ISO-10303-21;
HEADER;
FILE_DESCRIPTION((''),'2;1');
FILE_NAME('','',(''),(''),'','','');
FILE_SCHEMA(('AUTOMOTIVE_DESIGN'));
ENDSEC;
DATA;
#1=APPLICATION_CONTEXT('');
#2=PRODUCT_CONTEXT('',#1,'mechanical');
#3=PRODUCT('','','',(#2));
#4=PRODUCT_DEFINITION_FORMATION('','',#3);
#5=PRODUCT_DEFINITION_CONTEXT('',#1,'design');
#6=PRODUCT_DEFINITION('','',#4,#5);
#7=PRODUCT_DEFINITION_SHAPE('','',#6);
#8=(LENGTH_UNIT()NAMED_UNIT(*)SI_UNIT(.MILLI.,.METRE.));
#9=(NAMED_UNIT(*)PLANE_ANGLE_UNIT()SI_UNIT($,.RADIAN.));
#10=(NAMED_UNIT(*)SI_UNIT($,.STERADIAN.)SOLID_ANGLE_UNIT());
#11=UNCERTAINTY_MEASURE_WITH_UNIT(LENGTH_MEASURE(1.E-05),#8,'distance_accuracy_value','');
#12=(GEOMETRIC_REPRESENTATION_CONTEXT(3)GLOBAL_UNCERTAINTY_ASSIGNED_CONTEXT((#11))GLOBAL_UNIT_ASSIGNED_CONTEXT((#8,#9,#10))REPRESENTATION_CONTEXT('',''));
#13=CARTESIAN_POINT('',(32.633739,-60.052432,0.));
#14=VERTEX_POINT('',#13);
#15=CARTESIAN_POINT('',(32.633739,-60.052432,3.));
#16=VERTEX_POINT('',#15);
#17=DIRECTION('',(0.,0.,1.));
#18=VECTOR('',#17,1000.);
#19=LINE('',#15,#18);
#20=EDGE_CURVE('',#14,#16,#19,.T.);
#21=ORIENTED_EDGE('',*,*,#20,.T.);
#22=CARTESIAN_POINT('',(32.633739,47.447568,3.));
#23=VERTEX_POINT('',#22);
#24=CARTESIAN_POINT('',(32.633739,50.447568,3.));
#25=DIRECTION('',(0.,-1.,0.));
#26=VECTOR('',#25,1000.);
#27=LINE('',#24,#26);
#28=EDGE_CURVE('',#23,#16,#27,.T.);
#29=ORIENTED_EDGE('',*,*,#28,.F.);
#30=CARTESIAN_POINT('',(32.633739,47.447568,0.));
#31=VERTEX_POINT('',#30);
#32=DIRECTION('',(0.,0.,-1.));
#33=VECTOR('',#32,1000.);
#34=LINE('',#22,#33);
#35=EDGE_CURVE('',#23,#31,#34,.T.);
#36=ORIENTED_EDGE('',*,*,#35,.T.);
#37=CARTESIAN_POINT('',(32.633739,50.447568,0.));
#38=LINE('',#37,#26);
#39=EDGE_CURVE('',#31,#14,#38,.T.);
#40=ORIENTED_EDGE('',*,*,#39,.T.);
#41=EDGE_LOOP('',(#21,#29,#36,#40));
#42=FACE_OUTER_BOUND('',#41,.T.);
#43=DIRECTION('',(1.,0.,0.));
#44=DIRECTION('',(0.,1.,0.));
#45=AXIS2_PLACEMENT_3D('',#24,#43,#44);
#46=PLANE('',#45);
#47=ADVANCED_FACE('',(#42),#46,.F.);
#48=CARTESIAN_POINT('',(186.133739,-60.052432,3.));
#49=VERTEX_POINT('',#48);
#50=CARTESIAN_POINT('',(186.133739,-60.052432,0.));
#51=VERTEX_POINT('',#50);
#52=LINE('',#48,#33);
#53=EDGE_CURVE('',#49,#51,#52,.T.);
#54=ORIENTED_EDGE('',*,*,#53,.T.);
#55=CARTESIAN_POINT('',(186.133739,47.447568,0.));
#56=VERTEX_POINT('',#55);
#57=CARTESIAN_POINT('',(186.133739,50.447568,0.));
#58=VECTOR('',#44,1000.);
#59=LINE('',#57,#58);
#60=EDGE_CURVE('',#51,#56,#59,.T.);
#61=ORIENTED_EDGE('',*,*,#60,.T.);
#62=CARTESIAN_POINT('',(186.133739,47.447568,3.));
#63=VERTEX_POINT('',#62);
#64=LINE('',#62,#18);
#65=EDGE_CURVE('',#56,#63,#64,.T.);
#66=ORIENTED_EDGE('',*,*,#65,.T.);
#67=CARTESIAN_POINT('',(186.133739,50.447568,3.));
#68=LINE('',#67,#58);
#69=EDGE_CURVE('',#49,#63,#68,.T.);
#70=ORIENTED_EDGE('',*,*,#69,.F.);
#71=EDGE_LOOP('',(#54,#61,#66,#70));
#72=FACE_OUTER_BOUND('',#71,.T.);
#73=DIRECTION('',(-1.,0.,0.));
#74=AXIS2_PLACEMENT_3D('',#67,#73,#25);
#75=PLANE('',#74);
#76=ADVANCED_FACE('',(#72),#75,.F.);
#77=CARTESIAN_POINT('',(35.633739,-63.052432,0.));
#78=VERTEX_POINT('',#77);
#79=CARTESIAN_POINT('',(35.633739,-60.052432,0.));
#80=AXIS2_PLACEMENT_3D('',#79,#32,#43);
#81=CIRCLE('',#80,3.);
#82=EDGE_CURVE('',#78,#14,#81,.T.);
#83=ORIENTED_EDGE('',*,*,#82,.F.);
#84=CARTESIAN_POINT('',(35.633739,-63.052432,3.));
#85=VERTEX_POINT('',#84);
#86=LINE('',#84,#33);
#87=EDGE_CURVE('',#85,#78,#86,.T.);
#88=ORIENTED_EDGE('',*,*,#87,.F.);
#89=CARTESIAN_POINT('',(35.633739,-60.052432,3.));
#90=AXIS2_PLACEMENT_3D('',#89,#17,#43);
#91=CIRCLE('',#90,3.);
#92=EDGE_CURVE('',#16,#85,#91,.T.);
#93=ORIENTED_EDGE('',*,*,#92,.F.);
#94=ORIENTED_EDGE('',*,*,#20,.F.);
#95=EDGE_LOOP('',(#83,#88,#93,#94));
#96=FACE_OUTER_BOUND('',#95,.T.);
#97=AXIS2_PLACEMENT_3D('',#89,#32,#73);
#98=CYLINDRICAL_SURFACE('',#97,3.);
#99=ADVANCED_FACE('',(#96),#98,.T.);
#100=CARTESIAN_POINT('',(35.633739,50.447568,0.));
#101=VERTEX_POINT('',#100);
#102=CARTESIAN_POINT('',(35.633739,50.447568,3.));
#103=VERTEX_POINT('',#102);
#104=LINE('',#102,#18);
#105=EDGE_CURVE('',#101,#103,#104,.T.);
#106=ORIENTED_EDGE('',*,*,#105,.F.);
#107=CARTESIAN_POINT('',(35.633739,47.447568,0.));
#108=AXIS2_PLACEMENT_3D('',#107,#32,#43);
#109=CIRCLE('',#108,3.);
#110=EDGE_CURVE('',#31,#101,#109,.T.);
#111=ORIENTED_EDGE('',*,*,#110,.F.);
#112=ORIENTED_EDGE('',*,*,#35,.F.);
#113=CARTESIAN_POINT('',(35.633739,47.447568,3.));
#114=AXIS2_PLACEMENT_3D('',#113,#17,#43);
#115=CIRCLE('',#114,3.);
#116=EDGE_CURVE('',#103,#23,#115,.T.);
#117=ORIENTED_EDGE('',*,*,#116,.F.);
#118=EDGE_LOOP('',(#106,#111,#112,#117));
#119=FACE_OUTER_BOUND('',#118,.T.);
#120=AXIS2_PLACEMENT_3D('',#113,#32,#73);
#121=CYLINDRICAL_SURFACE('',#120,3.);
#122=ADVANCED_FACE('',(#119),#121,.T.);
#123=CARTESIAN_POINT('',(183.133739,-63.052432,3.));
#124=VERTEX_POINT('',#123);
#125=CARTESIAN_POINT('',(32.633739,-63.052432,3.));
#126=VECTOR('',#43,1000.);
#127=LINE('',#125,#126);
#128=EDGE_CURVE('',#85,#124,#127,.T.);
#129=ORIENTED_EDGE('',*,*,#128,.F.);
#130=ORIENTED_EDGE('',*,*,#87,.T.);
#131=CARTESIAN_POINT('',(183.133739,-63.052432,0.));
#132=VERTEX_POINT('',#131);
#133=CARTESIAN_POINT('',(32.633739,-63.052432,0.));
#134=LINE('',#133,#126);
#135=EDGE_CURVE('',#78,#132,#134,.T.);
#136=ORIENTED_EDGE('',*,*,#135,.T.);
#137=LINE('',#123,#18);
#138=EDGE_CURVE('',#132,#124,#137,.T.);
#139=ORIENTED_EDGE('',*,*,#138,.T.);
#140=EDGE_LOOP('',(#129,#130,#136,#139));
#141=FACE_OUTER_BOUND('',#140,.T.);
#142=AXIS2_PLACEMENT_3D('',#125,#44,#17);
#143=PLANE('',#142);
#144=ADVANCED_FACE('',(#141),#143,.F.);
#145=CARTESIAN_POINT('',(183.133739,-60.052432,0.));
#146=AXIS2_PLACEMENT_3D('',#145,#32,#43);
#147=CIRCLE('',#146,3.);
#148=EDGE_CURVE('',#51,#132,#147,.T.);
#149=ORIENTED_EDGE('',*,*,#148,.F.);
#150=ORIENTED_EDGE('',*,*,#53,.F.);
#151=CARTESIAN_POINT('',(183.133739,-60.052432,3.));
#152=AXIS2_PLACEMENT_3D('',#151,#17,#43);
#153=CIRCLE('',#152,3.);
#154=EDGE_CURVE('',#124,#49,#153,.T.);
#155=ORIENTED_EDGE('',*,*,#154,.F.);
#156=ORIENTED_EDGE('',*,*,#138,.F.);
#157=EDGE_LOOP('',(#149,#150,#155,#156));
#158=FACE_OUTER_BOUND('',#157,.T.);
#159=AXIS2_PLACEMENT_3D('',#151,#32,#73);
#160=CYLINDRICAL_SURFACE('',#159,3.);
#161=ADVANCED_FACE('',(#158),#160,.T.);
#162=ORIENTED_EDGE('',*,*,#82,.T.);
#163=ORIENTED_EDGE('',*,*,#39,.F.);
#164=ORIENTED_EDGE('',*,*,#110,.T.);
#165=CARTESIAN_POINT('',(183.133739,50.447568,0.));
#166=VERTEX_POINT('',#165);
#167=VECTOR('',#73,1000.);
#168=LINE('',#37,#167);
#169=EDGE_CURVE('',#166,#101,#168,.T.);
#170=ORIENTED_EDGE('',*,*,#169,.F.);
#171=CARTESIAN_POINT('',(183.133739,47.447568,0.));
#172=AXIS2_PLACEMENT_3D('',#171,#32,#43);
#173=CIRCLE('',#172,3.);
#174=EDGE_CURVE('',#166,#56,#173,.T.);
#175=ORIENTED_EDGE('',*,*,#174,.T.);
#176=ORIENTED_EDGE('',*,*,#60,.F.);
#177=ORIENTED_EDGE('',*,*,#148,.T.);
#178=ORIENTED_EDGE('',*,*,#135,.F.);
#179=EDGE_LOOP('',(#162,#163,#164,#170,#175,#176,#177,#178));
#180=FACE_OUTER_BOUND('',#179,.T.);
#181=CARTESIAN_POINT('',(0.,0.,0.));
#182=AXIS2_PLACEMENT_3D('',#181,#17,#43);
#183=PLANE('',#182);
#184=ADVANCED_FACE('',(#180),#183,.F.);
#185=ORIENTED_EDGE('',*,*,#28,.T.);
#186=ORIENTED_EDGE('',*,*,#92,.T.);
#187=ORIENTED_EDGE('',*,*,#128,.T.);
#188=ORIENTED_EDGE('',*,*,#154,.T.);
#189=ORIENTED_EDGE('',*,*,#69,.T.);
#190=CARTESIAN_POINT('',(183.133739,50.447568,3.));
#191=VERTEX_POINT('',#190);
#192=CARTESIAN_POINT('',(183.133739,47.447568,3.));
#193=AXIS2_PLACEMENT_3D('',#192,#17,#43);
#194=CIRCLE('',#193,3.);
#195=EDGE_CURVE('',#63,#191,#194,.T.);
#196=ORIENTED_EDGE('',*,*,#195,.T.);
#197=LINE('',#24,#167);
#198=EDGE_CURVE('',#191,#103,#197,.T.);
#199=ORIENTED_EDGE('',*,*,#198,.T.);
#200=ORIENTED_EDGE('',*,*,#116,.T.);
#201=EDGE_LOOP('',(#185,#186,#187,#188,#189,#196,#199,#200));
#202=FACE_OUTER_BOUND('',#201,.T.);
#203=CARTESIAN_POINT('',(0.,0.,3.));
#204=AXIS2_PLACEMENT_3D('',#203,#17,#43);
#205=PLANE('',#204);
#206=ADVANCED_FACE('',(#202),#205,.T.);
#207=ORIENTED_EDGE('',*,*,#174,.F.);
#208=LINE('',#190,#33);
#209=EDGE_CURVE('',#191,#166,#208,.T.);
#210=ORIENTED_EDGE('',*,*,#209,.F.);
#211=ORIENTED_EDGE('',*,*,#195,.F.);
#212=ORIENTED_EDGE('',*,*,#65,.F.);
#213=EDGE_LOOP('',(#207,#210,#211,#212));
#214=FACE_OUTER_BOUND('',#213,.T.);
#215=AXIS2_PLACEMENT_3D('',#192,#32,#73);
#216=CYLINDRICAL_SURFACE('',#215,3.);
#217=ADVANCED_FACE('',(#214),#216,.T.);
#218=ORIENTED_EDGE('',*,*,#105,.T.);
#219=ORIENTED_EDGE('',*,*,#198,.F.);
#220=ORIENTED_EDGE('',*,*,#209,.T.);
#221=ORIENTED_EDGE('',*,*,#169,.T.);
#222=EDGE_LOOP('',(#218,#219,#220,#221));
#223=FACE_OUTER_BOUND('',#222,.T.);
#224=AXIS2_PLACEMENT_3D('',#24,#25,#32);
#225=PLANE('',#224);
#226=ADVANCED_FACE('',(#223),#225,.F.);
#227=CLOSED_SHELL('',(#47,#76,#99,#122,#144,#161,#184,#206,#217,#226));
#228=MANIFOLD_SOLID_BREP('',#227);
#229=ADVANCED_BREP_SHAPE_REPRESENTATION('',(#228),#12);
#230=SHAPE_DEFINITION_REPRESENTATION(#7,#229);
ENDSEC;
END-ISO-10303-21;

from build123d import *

# Parameters (mm, degrees)
SKETCH_1_W      = 153.5
SKETCH_1_H      = 113.5
EXTRUDE_1_DEPTH = 3
FILLET_1_R      = 3


with BuildPart() as part:
    # 草图1 → 凸台-拉伸1 (new body)
    with BuildSketch(Plane.XY):
        with Locations((109.383738602, -6.302431611)):
            Rectangle(SKETCH_1_W, SKETCH_1_H)
    extrude(amount=EXTRUDE_1_DEPTH)

    # 圆角1
    fillet_1_edges = [part.edges().sort_by_distance(p)[0] for p in [
        (32.633738602, 50.447568389, 1.5),
        (186.133738602, 50.447568389, 1.5),
        (186.133738602, -63.052431611, 1.5),
        (32.633738602, -63.052431611, 1.5),
    ]]
    fillet(fillet_1_edges, radius=FILLET_1_R)


solid = part.part
